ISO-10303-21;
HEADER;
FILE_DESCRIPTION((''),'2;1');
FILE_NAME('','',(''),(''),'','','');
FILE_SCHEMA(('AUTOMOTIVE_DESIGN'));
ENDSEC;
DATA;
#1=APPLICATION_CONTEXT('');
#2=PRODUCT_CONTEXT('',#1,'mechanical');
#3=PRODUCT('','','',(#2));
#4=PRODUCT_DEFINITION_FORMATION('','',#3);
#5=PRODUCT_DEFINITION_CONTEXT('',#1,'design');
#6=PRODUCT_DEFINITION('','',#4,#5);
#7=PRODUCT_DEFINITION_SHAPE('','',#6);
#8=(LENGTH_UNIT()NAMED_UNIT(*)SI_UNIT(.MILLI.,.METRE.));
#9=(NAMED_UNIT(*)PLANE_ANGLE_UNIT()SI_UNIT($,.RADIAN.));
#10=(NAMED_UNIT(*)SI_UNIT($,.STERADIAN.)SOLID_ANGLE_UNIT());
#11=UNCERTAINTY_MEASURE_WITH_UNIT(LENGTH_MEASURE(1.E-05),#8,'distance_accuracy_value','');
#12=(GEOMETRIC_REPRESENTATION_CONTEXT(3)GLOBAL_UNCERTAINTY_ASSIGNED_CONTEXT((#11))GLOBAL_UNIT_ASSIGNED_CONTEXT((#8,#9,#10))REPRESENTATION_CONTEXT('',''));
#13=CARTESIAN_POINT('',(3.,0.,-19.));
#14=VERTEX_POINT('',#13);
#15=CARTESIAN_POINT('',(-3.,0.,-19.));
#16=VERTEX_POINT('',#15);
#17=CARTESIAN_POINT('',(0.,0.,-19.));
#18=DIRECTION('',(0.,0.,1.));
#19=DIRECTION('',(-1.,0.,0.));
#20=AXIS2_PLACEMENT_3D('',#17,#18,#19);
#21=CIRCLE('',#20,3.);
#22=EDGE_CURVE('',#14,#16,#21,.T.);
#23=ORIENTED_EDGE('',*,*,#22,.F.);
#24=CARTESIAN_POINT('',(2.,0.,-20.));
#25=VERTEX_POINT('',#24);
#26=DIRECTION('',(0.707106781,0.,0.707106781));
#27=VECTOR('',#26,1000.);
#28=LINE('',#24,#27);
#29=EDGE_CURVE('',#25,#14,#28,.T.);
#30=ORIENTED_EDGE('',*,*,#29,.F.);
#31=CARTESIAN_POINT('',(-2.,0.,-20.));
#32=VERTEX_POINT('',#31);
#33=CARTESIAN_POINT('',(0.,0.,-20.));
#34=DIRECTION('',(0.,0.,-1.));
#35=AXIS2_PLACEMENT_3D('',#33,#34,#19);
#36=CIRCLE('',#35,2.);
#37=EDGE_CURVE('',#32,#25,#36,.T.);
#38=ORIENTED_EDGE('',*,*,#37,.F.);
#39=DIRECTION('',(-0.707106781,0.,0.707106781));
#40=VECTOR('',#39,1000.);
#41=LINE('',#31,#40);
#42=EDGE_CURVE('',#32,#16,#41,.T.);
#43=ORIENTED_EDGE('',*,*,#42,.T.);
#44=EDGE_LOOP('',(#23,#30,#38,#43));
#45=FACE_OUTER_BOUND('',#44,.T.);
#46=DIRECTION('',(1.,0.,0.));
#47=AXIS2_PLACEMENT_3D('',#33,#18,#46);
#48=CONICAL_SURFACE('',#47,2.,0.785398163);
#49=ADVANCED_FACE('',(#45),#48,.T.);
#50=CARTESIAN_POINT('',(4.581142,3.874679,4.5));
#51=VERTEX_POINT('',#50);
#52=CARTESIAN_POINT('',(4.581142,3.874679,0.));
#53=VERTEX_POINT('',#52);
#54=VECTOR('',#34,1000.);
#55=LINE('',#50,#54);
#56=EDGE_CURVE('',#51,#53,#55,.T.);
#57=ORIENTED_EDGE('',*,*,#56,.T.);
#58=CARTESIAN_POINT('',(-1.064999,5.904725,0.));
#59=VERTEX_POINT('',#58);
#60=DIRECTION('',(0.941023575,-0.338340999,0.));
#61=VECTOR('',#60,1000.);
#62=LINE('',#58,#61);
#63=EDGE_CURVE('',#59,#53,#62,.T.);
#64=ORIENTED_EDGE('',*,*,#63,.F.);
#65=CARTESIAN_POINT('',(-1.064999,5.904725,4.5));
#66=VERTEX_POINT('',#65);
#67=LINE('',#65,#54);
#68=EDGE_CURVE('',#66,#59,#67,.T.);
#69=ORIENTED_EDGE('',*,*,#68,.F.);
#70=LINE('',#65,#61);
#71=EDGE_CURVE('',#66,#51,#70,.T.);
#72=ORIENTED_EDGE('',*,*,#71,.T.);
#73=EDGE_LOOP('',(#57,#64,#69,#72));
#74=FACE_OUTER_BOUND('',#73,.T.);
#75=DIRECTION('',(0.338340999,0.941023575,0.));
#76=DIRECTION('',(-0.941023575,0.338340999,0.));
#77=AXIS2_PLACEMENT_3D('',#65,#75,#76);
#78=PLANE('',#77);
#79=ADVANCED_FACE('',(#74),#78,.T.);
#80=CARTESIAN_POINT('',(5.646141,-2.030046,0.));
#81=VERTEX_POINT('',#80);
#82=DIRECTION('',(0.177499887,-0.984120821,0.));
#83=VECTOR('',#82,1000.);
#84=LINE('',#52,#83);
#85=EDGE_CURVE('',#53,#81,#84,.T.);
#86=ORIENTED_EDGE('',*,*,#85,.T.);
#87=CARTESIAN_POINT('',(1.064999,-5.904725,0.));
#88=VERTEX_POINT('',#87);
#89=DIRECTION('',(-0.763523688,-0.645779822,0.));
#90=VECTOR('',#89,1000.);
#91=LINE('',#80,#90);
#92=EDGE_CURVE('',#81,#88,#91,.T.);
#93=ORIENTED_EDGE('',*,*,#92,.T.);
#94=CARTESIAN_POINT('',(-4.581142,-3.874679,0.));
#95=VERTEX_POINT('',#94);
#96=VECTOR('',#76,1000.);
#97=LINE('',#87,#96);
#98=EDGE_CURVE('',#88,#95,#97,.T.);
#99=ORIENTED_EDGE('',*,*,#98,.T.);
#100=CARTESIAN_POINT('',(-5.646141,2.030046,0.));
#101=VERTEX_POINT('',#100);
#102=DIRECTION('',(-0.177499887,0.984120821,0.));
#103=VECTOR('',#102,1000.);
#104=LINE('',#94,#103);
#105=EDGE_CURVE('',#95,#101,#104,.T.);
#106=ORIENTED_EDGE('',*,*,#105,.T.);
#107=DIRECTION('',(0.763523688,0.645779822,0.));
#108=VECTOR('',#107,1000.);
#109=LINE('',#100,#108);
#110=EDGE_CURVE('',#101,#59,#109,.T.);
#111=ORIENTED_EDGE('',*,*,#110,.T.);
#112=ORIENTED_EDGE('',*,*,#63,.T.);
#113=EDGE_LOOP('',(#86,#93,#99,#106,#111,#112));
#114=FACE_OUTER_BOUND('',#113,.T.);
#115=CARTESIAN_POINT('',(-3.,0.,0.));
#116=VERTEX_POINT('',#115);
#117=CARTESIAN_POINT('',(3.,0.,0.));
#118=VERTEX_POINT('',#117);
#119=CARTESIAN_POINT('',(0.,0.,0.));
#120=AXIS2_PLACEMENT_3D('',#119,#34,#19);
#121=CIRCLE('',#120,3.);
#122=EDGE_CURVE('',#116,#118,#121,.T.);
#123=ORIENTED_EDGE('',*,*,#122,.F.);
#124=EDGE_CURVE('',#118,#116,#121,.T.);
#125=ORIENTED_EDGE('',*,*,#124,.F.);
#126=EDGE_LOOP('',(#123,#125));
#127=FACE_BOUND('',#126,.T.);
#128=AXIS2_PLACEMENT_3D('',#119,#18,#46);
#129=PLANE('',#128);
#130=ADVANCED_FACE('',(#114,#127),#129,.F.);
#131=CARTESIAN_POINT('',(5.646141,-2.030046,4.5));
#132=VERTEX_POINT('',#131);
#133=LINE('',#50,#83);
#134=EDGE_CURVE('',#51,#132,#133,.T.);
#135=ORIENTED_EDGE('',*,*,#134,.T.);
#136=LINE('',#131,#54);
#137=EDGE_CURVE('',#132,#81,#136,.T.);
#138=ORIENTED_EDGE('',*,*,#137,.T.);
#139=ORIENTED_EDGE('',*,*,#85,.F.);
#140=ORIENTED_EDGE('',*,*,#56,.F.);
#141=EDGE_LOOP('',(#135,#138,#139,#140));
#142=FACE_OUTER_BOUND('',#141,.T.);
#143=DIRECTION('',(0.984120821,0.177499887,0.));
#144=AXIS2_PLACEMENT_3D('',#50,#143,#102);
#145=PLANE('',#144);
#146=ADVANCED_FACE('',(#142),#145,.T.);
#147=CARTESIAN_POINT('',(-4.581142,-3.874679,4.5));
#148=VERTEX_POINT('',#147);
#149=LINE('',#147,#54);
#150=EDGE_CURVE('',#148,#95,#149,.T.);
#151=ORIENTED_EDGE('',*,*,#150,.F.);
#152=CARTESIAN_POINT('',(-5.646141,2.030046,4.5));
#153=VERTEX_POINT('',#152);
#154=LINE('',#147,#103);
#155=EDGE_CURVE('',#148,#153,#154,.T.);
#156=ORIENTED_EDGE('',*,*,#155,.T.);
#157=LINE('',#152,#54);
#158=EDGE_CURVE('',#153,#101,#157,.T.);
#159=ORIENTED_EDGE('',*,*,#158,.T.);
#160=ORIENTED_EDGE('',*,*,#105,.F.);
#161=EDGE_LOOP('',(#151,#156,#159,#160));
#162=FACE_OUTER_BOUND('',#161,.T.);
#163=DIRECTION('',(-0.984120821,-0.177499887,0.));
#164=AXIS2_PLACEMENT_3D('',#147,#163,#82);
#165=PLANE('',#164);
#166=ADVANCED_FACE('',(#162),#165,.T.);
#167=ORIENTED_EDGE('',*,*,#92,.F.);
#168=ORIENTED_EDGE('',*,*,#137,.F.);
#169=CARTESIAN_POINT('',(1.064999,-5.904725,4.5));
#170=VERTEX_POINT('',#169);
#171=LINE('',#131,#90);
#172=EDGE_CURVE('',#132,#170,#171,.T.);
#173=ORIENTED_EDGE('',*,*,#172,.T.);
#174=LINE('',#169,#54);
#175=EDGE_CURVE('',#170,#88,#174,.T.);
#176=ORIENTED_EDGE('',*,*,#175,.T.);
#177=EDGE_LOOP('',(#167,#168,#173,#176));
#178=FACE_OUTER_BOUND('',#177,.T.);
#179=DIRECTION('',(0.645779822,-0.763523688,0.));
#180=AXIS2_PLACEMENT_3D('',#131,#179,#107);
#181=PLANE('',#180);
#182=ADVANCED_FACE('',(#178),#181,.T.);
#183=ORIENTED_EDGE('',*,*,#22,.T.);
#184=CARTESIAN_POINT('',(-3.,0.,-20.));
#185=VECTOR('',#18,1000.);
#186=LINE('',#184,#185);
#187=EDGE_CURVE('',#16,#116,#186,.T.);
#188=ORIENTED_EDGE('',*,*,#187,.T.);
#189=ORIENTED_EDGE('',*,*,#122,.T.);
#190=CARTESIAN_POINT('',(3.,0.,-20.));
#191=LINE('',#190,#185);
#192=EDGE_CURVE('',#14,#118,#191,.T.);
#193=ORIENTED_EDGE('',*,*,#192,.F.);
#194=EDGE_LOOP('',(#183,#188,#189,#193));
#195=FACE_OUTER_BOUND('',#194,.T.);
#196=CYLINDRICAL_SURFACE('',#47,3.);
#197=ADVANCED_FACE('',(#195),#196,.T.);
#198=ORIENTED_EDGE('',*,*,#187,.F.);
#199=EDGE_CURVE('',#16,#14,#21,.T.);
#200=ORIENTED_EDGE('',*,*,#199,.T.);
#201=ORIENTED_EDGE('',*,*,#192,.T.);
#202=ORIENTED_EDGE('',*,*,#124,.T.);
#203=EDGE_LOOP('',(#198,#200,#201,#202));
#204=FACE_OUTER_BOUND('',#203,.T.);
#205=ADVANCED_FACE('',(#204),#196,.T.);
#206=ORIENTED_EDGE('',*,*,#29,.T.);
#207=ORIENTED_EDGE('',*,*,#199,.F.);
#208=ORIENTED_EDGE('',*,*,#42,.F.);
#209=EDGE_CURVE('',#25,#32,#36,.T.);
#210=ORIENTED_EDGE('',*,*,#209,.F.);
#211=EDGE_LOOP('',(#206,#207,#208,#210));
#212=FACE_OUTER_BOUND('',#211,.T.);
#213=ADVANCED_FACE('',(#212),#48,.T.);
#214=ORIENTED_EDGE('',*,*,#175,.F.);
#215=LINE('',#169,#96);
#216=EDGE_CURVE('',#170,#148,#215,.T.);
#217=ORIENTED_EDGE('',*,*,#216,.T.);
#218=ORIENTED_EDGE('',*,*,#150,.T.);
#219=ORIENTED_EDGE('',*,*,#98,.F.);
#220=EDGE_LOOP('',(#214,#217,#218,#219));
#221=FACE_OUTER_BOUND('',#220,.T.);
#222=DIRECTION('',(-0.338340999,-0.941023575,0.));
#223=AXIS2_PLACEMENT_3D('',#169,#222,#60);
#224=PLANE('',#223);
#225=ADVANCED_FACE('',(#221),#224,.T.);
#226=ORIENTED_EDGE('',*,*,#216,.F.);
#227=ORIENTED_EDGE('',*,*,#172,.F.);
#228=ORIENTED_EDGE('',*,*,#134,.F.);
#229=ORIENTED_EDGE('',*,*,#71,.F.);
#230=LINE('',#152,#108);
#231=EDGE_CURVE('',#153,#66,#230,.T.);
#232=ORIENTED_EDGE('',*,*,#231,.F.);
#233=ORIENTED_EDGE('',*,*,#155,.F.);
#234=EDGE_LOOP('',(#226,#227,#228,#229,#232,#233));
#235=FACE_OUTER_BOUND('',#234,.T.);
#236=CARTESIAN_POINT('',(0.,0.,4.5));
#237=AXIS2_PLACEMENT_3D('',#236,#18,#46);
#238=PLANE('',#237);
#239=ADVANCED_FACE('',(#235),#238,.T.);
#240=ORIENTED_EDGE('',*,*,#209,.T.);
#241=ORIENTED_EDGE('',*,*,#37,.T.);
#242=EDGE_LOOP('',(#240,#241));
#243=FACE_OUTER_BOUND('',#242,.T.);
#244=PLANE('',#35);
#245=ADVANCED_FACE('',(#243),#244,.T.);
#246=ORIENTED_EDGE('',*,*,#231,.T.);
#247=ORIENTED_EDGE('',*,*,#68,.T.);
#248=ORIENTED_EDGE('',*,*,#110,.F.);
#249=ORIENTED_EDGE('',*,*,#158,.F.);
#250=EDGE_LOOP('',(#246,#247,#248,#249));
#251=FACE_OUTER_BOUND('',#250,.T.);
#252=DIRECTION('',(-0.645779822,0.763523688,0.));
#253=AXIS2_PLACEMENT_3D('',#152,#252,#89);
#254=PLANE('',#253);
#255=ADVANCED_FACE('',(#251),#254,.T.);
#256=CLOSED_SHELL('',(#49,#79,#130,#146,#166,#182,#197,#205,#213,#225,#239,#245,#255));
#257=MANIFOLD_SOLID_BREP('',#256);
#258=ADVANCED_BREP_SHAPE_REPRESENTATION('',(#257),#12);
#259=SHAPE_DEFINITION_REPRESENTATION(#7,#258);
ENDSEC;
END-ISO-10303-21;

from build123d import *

# Parameters (mm, degrees)
SKETCH1_R           = 6
BOSS_EXTRUDE1_DEPTH = 4.5
SKETCH2_OUTSIDE_W   = 17.512
SKETCH2_OUTSIDE_H   = 17.512
CUT_EXTRUDE1_DEPTH  = 4.5
SKETCH3_R           = 3
BOSS_EXTRUDE2_DEPTH = 20
CHAMFER2_SIZE       = 1


with BuildPart() as part:
    # Sketch1 → Boss-Extrude1 (new body)
    with BuildSketch(Plane.XY):
        Circle(SKETCH1_R)
    extrude(amount=BOSS_EXTRUDE1_DEPTH)

    # Sketch2 outside → Cut-Extrude1 (cut)
    with BuildSketch(Plane(origin=(0, 0, 0), x_dir=(-1, 0, 0), z_dir=(0, 0, -1))):
        Rectangle(SKETCH2_OUTSIDE_W, SKETCH2_OUTSIDE_H)
        Polygon((4.581142128, -3.874678929), (5.646141448, 2.030045997), (1.06499932, 5.904724926), (-4.581142128, 3.874678929), (-5.646141448, -2.030045997), (-1.06499932, -5.904724926), align=None, mode=Mode.SUBTRACT)
    extrude(amount=-CUT_EXTRUDE1_DEPTH, mode=Mode.SUBTRACT)

    # Sketch3 → Boss-Extrude2 (add)
    with BuildSketch(Plane(origin=(0, 0, 0), x_dir=(-1, 0, 0), z_dir=(0, 0, -1))):
        Circle(SKETCH3_R)
    extrude(amount=BOSS_EXTRUDE2_DEPTH)

    # Chamfer2
    chamfer2_edges = [part.edges().sort_by_distance(p)[0] for p in [
        (3, 0, -20),
    ]]
    chamfer(chamfer2_edges, length=CHAMFER2_SIZE)


solid = part.part
